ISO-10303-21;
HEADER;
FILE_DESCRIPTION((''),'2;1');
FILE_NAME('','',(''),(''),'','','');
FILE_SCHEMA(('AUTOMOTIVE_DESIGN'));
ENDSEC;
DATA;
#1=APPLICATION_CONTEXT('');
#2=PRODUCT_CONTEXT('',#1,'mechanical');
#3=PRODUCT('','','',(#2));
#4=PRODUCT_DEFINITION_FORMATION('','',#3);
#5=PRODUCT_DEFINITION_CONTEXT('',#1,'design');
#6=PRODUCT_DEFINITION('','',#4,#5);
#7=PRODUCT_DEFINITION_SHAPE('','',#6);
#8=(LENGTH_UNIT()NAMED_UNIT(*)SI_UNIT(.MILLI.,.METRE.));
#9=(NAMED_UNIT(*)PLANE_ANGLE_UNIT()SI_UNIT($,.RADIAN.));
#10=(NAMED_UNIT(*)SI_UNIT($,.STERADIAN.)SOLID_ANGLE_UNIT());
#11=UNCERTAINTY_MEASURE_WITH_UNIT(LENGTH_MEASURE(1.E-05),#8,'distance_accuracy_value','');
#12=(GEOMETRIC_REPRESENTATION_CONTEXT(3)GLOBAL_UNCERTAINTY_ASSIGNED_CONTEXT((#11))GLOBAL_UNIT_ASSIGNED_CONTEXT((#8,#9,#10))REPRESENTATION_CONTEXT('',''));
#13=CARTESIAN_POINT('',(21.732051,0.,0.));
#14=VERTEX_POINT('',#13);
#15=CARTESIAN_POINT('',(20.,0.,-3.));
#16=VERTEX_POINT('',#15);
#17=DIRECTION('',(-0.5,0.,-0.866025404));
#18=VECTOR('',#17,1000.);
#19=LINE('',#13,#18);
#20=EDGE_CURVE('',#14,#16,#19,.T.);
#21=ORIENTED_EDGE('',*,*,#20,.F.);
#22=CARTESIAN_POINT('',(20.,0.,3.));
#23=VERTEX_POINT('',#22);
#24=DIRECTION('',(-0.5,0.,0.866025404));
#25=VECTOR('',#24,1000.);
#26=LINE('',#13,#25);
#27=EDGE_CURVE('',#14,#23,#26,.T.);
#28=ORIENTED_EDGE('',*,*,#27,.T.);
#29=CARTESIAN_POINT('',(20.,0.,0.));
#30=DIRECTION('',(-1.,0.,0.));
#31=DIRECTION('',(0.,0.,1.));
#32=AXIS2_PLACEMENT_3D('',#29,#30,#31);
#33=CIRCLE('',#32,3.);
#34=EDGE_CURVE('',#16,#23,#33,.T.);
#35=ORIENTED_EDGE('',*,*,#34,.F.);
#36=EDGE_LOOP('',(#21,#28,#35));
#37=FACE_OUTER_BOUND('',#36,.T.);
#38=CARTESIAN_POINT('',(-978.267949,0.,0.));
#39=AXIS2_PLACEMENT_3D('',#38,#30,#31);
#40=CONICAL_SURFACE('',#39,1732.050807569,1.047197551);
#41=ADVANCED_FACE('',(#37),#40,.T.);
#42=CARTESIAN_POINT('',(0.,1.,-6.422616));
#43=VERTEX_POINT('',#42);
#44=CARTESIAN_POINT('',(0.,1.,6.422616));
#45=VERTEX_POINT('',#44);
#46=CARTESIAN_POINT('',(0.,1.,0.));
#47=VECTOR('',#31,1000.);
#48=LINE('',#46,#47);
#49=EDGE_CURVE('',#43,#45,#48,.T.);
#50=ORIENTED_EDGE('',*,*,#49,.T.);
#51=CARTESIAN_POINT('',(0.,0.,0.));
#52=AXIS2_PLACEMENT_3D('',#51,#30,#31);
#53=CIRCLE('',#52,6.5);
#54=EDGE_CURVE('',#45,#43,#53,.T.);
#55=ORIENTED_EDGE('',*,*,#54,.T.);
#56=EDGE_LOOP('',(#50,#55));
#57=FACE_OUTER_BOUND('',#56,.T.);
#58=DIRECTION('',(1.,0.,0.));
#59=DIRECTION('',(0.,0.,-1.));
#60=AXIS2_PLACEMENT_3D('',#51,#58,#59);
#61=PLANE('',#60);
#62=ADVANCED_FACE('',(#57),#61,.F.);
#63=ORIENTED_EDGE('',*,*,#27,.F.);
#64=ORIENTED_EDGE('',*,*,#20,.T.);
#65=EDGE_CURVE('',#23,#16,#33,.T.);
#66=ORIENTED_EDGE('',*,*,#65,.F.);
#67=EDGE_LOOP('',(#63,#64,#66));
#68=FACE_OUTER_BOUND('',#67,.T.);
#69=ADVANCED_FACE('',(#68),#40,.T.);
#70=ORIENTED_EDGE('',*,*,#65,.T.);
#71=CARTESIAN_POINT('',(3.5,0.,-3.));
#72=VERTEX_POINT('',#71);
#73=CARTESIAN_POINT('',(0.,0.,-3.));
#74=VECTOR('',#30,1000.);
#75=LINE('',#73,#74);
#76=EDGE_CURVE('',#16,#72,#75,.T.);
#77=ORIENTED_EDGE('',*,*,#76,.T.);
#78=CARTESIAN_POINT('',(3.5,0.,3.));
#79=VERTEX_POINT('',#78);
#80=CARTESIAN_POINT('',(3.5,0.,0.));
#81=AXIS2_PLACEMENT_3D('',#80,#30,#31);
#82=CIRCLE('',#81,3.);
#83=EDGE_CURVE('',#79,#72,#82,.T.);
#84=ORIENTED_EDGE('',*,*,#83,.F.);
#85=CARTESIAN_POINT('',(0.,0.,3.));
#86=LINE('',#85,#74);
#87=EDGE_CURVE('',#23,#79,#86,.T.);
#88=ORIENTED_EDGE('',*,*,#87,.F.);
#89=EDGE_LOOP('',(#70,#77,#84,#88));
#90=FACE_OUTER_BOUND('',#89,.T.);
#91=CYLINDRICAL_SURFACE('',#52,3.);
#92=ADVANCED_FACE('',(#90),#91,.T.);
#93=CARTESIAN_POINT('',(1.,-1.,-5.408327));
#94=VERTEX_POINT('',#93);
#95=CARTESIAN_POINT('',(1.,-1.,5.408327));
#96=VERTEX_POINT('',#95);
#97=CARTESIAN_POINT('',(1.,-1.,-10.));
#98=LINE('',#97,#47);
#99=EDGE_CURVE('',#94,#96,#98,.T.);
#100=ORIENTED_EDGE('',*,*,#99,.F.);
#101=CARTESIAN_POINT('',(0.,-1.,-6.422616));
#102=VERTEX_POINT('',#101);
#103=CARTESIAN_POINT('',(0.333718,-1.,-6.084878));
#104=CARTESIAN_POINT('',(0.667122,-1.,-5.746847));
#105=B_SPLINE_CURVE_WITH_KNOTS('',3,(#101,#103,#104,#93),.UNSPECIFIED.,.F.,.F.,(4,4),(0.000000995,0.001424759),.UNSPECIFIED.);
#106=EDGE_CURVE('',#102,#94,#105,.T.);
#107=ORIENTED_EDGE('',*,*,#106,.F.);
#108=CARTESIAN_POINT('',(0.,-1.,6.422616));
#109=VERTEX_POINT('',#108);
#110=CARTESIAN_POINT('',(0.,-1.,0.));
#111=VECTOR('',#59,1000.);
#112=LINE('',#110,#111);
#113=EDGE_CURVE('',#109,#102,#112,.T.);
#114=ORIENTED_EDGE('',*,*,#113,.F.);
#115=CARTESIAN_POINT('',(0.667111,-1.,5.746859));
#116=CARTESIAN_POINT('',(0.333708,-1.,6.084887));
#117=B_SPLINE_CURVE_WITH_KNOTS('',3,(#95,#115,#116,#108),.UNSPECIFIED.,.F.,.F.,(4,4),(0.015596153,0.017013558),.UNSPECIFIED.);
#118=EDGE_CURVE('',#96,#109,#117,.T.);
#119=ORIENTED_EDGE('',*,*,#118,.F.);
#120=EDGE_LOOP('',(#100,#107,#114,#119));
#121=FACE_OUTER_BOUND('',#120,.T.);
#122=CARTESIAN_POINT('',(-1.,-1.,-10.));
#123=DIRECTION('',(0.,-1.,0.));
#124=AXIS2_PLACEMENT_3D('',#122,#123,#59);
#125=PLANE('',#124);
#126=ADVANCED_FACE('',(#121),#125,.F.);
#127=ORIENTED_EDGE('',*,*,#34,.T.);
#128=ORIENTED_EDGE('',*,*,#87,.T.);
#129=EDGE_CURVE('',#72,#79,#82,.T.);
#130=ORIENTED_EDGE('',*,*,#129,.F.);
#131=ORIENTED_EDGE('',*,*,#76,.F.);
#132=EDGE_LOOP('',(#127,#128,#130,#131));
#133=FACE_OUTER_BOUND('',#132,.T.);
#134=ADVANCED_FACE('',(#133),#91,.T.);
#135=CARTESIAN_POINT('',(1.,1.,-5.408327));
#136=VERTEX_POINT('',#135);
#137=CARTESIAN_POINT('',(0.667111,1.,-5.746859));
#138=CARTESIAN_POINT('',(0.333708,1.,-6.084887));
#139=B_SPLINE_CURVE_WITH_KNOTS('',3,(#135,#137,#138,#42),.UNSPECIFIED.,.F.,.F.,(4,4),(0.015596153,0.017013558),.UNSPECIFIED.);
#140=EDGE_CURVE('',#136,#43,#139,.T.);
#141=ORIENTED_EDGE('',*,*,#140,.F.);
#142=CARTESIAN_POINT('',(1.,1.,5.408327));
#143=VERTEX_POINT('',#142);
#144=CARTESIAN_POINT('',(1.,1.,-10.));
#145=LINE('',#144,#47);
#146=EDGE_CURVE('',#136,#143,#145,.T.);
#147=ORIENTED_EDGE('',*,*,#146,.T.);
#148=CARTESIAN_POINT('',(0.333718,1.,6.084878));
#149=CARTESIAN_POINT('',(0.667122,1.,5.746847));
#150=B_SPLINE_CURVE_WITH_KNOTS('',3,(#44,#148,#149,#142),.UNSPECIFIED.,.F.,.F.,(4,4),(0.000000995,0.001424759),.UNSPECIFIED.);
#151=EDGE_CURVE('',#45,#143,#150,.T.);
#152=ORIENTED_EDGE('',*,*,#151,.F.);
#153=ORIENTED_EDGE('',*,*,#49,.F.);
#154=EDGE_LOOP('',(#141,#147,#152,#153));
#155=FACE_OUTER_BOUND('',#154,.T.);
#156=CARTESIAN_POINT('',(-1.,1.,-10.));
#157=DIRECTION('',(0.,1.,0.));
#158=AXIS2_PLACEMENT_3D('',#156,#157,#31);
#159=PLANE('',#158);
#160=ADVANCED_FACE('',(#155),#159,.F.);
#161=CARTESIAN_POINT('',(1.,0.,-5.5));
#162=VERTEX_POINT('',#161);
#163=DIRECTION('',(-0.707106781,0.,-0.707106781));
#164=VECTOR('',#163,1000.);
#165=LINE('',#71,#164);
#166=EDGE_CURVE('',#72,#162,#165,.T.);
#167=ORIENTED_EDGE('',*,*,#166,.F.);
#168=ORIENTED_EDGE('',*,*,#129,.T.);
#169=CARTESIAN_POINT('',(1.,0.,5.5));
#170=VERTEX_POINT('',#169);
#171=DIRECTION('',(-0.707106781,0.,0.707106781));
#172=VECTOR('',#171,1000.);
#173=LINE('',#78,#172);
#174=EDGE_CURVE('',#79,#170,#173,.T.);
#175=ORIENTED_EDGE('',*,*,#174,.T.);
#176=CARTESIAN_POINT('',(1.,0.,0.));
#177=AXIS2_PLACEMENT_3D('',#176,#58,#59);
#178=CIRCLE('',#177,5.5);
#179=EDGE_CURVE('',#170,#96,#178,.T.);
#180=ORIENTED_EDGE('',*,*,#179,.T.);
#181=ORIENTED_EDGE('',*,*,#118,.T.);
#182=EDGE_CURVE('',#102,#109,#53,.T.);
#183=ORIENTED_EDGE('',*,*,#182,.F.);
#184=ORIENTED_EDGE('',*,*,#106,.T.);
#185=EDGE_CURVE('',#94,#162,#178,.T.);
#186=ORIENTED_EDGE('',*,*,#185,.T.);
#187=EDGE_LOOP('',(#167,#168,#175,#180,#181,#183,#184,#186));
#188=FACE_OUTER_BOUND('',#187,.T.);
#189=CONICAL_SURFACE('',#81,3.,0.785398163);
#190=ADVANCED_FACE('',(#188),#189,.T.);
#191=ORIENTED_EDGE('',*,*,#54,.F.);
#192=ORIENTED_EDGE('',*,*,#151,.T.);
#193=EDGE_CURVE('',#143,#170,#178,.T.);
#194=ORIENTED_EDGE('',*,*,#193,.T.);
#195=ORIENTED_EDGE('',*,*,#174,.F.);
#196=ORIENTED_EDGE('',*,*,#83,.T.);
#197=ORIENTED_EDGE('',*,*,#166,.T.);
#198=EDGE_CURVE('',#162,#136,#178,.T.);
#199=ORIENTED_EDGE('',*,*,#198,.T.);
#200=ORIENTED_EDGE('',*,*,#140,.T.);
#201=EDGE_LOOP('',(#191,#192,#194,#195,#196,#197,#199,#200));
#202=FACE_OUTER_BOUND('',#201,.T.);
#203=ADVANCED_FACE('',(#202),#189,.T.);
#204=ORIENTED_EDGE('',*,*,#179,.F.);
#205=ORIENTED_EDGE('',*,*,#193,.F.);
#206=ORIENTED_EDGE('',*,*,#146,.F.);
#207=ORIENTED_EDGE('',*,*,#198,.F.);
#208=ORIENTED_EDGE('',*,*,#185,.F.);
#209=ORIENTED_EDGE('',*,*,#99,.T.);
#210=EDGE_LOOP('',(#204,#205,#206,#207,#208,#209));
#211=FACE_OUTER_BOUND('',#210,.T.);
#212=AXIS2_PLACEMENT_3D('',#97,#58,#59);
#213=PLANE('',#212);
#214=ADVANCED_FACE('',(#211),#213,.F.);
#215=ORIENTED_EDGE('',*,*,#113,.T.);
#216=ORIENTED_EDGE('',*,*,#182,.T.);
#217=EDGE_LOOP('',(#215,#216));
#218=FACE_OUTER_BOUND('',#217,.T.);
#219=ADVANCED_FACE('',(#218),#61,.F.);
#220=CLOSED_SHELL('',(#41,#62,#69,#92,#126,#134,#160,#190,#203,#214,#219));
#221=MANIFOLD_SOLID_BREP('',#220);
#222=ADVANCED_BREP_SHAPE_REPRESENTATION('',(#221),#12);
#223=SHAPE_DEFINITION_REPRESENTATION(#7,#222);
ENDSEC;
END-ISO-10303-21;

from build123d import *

# Parameters (mm, degrees)
CUT_EXTRUDE1_DEPTH      = 12
CUT_EXTRUDE1_DEPTH_BACK = 10
SKETCH2_W               = 2
SKETCH2_H               = 2


with BuildPart() as part:
    # Sketch1 → Revolve1 (revolve)
    with BuildSketch(Plane.XY, mode=Mode.PRIVATE) as revolve1_sk:
        Polygon((0, 0), (0, 6.5), (3.5, 3), (20, 3), (21.732050808, 0), align=None)
    revolve(revolve1_sk.sketch.rotate(Axis((0, 0, 0), (1, 0, 0)), 90), axis=Axis((0, 0, 0), (1, 0, 0)))

    # Sketch2 → Cut-Extrude1 (cut, two sides: drawn at the far end of the back side and taken through both)
    with BuildSketch(Plane.XY.offset(-CUT_EXTRUDE1_DEPTH_BACK)):
        Rectangle(SKETCH2_W, SKETCH2_H)
    extrude(amount=CUT_EXTRUDE1_DEPTH + CUT_EXTRUDE1_DEPTH_BACK, mode=Mode.SUBTRACT)


solid = part.part
